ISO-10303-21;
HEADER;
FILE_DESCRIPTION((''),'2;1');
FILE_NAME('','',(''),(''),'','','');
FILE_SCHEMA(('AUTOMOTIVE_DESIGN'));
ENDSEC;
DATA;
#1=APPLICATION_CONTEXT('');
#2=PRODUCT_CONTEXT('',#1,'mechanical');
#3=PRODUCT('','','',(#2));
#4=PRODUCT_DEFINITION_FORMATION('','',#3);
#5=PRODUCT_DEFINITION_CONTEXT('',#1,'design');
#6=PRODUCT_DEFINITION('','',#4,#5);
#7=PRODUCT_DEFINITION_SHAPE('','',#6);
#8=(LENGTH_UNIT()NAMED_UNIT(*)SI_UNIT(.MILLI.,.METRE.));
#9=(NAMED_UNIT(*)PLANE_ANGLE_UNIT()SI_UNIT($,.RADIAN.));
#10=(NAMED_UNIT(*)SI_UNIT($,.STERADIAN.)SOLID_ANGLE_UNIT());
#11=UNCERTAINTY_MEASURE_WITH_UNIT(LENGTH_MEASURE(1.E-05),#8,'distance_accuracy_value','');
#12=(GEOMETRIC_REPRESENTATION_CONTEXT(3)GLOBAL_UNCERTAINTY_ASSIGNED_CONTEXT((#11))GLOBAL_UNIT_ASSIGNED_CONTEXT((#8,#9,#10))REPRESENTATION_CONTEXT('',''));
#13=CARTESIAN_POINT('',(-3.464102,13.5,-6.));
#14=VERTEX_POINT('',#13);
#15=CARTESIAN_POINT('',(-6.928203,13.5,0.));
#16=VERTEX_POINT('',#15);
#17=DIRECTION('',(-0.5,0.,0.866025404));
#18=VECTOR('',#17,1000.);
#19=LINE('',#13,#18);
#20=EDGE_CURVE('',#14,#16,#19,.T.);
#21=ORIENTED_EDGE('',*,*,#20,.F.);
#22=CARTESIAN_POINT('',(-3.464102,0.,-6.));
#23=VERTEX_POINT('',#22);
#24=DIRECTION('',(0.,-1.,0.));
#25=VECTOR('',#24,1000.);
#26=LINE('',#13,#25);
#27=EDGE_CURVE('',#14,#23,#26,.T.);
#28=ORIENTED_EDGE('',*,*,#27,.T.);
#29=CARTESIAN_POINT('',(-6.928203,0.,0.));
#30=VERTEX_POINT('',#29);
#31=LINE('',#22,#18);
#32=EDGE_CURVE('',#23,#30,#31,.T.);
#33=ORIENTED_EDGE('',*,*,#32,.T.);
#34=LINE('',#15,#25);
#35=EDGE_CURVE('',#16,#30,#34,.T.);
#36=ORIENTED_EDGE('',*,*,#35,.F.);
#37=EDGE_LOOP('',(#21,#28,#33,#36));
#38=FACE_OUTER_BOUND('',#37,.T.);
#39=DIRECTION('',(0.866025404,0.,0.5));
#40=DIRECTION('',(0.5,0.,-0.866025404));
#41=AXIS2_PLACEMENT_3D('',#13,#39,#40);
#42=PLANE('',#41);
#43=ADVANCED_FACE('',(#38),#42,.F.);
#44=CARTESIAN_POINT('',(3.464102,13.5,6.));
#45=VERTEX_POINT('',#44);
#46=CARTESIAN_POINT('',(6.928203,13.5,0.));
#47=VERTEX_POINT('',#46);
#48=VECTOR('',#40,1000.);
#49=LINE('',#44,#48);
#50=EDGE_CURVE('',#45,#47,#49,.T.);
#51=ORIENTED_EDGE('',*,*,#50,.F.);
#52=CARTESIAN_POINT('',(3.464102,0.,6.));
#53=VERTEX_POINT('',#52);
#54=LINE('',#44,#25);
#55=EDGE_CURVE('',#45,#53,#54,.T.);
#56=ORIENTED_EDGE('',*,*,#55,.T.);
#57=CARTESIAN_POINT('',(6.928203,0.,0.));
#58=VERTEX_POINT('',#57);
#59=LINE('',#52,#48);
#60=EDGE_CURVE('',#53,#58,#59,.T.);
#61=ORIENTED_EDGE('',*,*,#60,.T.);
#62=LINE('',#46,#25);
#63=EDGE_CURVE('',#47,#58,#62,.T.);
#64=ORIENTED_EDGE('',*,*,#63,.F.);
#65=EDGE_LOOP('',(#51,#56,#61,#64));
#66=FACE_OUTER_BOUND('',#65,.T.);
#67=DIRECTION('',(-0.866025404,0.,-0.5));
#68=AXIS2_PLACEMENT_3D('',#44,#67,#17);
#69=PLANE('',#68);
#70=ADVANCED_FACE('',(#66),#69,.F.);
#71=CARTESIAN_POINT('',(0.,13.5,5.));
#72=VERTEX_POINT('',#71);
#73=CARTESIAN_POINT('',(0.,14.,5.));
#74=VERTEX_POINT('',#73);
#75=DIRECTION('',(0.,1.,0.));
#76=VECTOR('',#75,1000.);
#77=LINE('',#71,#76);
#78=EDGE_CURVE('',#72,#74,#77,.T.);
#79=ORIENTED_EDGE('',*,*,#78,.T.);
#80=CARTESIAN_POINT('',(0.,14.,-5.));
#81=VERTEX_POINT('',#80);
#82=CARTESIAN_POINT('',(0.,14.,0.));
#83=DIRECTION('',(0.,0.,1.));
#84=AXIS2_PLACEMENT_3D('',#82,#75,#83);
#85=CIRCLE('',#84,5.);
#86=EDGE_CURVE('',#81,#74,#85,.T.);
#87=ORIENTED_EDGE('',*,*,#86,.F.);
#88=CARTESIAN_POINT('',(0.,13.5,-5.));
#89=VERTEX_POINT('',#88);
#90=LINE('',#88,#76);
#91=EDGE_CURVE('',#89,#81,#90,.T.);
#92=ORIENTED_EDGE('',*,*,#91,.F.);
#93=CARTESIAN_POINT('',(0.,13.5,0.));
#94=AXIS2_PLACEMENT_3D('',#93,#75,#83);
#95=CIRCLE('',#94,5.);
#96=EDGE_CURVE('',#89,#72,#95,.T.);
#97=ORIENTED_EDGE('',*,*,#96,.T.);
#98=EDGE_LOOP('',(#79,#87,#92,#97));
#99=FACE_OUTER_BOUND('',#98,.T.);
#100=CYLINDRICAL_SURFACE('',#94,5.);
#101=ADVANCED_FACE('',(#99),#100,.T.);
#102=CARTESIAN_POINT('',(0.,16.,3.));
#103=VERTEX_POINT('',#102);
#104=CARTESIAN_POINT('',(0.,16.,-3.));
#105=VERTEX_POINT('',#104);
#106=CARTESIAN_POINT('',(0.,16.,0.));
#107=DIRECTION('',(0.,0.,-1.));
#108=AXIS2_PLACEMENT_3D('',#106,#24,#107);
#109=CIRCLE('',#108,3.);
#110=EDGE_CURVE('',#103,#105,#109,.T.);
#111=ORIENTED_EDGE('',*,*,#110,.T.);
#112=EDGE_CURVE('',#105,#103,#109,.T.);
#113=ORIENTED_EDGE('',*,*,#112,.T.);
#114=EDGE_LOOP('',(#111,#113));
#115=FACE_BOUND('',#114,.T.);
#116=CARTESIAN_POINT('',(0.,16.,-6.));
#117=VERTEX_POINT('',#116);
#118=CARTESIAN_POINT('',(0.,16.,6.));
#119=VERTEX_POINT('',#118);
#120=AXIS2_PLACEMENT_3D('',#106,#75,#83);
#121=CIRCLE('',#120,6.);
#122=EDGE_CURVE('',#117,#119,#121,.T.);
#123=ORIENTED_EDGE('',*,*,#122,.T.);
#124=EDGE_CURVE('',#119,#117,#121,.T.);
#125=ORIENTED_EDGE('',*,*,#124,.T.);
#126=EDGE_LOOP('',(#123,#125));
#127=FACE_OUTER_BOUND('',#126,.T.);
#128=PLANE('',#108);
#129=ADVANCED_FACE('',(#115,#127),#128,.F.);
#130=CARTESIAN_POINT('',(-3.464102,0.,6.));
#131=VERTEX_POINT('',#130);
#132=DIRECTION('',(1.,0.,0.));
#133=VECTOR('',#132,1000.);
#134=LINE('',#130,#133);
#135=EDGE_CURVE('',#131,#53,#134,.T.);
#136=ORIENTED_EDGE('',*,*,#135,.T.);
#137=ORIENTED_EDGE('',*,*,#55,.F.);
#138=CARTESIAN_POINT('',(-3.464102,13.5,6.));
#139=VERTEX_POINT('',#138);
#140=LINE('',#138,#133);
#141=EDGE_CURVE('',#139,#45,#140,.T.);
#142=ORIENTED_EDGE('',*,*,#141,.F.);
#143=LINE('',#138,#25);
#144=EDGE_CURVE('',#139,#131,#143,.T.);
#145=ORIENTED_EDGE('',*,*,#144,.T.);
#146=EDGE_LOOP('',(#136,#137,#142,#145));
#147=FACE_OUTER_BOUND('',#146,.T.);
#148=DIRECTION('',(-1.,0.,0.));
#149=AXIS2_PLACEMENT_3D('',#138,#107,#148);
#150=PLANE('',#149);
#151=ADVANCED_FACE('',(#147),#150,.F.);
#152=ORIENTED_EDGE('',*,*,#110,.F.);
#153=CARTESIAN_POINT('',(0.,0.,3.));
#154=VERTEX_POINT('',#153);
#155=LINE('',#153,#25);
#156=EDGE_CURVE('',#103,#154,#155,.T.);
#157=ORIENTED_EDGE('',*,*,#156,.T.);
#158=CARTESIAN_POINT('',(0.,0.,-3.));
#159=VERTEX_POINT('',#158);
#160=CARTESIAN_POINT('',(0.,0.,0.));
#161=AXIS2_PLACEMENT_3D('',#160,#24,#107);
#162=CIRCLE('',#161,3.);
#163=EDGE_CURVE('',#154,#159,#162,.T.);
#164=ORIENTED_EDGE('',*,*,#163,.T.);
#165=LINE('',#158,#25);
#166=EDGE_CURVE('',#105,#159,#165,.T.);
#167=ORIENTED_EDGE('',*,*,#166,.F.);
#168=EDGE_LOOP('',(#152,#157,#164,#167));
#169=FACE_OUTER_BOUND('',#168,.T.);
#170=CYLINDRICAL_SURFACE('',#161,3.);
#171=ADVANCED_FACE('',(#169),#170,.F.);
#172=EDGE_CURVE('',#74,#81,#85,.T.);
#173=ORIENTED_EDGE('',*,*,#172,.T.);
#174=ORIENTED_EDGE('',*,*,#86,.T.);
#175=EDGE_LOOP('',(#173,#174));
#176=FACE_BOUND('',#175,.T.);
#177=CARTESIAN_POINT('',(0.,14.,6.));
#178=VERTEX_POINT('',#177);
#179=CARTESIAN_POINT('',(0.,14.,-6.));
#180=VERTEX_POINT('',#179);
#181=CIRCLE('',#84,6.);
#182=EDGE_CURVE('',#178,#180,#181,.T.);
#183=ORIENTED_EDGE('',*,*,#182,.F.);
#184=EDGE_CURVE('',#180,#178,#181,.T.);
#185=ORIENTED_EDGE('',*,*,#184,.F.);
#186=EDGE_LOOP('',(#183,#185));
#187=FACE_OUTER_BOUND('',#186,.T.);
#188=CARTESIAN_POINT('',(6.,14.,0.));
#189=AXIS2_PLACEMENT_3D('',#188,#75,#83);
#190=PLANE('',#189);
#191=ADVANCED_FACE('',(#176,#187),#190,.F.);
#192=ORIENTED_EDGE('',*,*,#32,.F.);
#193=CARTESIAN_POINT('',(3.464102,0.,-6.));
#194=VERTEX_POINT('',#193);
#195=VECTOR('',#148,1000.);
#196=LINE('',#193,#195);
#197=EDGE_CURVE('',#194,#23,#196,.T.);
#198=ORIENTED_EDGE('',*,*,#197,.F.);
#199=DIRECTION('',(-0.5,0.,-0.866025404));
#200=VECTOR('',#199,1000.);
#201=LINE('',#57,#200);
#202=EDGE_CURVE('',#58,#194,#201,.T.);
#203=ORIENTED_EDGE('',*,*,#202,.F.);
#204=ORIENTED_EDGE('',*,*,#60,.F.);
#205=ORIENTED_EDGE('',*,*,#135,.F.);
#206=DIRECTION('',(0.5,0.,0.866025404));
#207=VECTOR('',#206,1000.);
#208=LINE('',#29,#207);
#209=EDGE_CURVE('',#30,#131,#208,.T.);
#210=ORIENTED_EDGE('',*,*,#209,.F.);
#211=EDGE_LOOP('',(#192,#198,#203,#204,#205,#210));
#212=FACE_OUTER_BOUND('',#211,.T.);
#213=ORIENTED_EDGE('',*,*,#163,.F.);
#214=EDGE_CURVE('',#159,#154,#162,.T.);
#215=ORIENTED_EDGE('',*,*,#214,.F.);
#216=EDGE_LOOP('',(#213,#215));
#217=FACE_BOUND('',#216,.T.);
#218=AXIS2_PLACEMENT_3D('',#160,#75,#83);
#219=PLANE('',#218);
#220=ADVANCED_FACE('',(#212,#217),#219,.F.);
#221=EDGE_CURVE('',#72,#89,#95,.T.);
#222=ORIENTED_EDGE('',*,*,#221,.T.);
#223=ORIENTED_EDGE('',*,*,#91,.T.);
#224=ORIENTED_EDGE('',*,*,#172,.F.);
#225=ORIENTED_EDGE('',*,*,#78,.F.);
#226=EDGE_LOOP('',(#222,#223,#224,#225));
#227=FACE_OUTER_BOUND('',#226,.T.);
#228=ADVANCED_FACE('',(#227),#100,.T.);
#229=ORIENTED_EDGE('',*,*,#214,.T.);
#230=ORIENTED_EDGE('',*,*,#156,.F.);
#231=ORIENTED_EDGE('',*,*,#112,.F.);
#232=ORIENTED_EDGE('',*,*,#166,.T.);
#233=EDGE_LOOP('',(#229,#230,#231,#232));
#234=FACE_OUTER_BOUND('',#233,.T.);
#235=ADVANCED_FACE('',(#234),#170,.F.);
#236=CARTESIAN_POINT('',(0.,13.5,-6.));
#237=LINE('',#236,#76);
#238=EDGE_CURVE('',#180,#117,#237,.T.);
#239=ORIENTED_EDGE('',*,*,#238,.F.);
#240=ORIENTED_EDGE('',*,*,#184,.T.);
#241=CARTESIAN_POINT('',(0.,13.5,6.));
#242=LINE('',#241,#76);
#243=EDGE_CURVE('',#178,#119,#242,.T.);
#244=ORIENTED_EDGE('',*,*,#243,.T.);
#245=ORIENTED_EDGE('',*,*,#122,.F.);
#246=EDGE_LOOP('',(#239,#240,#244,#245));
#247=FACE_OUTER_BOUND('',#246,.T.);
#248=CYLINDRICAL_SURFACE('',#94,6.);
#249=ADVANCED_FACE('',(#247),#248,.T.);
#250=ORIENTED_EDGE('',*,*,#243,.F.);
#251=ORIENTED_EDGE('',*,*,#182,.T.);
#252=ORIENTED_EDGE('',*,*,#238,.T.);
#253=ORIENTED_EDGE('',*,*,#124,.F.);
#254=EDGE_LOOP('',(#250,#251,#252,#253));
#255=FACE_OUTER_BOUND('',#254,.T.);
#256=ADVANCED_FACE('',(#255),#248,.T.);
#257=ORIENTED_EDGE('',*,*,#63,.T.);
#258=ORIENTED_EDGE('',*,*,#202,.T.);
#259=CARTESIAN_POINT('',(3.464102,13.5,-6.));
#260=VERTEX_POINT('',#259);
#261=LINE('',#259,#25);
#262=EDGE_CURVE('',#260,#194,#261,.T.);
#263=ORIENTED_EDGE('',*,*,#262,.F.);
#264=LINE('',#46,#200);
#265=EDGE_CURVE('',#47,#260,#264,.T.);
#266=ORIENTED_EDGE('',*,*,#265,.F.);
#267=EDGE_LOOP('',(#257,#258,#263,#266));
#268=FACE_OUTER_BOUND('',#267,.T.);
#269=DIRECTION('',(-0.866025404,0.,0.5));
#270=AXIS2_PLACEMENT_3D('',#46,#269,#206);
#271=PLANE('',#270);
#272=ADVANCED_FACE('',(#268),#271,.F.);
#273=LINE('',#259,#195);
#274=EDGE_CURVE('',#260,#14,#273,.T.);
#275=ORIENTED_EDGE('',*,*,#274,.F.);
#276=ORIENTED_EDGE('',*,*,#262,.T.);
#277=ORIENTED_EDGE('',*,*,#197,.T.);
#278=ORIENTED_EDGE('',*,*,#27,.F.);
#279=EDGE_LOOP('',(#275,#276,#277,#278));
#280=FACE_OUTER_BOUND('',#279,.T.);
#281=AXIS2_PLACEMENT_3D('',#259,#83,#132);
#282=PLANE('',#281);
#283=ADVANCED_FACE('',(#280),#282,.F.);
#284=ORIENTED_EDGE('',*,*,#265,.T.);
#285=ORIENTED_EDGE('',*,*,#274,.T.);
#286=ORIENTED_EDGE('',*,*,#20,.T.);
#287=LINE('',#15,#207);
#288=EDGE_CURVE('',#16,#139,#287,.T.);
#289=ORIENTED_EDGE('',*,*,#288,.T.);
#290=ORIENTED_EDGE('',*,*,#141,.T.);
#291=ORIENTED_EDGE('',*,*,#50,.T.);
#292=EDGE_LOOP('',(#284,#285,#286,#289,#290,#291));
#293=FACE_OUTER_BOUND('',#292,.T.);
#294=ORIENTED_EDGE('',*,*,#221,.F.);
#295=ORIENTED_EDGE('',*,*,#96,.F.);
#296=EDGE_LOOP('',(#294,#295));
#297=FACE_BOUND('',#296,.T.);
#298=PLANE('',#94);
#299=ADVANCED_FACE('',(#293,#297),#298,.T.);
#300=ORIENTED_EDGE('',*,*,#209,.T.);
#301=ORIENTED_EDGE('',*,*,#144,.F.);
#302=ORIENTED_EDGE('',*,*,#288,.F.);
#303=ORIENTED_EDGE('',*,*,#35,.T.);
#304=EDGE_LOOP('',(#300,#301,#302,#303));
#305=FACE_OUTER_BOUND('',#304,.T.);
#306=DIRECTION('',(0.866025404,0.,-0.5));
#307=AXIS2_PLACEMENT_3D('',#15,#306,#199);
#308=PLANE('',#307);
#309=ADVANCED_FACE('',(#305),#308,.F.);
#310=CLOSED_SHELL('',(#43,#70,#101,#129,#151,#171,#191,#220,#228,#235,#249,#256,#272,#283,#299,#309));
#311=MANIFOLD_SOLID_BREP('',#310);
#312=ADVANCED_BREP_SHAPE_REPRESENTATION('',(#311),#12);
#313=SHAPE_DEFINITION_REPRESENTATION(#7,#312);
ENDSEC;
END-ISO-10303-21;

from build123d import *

# Parameters (mm, degrees)
BOSS_EXTRUDE1_DEPTH = 13.5
HOLE1_D             = 6


with BuildPart() as part:
    # Sketch1 → Boss-Extrude1 (new body)
    with BuildSketch(Plane(origin=(0, 0, 0), x_dir=(1, 0, 0), z_dir=(0, 1, 0))):
        Polygon((-6.92820323, 0), (-3.464101615, -6), (3.464101615, -6), (6.92820323, 0), (3.464101615, 6), (-3.464101615, 6), align=None)
    extrude(amount=BOSS_EXTRUDE1_DEPTH)

    # Sketch2 → Revolve1 (revolve)
    with BuildSketch(Plane.XY, mode=Mode.PRIVATE) as revolve1_sk:
        Polygon((0, 16), (6, 16), (6, 14), (5, 14), (5, 13.5), (0, 13.5), align=None)
    revolve(revolve1_sk.sketch.rotate(Axis((0, 13.5, 0), (0, 1, 0)), 270), axis=Axis((0, 13.5, 0), (0, 1, 0)))

    # Hole1 (through all)
    with Locations(Plane(origin=(0, 0, 0), x_dir=(-1, 0, 0), z_dir=(0, -1, 0))):
        with Locations((0, 0)):
            Hole(HOLE1_D / 2)


solid = part.part
